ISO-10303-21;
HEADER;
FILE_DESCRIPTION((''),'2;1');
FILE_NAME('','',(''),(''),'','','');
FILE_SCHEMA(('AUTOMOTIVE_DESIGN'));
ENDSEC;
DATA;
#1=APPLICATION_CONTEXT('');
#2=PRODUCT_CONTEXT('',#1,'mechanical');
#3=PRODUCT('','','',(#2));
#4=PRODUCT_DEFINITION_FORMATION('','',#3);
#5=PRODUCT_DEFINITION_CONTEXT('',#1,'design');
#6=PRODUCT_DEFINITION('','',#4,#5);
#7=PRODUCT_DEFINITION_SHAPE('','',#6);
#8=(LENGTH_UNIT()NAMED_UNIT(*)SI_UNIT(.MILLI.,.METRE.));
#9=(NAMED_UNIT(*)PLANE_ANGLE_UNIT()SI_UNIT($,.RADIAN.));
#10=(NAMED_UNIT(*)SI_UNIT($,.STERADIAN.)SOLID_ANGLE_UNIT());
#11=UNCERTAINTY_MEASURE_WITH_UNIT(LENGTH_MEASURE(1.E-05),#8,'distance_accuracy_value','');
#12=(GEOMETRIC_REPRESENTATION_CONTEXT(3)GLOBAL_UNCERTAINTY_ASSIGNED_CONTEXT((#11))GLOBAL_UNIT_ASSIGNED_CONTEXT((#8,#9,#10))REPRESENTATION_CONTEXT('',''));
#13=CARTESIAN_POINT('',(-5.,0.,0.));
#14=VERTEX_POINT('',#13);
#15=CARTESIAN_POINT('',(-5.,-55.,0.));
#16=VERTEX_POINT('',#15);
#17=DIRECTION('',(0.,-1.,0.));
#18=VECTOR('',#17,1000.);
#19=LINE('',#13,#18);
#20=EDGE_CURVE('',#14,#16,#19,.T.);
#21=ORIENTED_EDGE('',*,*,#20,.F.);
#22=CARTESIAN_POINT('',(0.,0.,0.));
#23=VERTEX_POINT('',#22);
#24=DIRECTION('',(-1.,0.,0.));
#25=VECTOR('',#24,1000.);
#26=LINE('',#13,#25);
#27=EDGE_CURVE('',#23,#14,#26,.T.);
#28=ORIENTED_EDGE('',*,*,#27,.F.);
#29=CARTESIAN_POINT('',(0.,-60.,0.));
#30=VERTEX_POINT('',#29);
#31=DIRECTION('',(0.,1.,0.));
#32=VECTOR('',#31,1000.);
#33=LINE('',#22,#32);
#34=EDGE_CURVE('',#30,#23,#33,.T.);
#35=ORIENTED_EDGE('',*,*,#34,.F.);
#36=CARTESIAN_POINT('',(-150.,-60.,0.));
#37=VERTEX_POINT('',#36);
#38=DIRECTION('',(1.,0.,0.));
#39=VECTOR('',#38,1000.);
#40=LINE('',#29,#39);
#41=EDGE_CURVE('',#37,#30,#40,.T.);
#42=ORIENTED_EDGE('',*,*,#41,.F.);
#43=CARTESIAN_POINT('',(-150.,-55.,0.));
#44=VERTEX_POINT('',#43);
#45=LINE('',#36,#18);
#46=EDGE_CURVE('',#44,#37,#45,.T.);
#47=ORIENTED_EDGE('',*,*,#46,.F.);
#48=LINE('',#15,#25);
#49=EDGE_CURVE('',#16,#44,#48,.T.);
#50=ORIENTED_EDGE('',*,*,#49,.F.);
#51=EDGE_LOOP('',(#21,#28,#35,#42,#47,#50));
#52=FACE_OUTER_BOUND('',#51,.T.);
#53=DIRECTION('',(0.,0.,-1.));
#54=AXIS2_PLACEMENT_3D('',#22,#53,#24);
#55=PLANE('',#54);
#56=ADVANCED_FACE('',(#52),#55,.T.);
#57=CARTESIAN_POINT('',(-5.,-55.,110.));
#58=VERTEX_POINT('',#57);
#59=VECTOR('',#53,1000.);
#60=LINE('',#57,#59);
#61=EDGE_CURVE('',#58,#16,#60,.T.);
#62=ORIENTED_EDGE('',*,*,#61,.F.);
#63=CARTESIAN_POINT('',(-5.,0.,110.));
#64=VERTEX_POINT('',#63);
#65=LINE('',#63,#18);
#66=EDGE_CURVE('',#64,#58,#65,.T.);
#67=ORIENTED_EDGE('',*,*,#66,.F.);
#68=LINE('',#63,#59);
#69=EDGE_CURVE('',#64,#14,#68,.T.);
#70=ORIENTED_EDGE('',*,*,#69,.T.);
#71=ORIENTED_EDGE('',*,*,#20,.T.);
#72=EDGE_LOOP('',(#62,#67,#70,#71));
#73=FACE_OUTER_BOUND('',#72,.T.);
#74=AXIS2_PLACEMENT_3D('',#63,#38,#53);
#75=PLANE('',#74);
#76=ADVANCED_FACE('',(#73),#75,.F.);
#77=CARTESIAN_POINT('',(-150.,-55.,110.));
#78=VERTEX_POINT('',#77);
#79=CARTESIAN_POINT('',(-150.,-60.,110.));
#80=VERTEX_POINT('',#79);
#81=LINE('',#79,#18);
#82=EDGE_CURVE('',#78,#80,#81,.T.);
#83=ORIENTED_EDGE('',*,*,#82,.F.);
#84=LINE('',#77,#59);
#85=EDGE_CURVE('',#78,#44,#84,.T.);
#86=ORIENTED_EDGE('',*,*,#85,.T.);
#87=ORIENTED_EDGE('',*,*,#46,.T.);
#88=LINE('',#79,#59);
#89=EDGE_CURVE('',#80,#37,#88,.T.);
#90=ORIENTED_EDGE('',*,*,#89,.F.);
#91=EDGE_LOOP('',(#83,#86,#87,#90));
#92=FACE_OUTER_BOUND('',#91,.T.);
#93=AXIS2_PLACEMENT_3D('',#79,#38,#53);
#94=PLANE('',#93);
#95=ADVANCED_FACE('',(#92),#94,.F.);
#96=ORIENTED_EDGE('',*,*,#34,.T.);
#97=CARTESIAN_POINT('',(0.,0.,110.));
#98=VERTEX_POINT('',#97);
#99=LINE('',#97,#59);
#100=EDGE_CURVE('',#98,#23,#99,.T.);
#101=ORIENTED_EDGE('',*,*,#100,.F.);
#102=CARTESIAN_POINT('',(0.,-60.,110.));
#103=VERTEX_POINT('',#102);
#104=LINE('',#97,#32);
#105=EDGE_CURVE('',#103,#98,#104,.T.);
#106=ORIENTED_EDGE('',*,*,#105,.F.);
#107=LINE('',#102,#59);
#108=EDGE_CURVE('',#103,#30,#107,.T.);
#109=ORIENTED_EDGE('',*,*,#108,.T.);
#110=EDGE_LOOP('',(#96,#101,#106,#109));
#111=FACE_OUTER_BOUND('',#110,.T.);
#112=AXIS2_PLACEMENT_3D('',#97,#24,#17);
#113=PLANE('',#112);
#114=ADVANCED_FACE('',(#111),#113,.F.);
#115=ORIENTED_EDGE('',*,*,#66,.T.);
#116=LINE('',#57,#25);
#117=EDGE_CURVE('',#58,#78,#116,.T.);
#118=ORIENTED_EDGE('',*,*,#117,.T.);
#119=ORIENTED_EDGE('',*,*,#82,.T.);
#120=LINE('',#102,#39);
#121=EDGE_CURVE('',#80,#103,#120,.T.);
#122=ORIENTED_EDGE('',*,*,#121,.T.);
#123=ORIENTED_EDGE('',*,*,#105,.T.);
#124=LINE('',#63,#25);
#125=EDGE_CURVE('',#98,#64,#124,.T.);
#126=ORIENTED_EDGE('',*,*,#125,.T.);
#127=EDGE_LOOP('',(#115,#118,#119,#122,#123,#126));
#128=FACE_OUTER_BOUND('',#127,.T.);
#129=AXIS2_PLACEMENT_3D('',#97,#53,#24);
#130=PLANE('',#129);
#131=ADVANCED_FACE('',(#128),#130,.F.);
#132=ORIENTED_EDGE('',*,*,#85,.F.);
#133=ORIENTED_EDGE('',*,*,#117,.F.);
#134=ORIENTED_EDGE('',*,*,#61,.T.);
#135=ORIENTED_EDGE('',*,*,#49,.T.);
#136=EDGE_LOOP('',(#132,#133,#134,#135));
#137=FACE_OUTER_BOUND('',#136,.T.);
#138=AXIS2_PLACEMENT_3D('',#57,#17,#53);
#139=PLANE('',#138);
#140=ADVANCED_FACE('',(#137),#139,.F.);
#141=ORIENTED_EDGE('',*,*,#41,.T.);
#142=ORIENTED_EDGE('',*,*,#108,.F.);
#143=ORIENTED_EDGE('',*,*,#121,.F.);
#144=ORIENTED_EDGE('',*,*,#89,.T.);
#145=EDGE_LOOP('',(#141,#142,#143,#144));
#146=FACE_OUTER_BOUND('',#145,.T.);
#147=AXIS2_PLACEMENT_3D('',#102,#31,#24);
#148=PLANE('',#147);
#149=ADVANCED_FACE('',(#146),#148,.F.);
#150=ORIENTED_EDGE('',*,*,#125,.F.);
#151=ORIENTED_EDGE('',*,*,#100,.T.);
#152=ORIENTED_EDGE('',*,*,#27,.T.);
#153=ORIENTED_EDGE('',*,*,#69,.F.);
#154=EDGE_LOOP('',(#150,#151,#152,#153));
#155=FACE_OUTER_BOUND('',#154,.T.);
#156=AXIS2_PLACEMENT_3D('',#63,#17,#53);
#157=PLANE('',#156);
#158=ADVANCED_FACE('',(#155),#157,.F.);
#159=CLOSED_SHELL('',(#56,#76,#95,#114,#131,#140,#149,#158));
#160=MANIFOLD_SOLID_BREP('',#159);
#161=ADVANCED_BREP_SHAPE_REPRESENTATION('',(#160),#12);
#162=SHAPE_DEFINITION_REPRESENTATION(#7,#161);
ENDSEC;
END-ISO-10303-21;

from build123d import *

# Parameters (mm, degrees)
EXTRUDE_1_DEPTH = 110


with BuildPart() as part:
    # 草图1 → 凸台-拉伸1 (new body)
    with BuildSketch(Plane.XY):
        Polygon((0, 0), (0, -60), (-150, -60), (-150, -55), (-5, -55), (-5, 0), align=None)
    extrude(amount=EXTRUDE_1_DEPTH)


solid = part.part
